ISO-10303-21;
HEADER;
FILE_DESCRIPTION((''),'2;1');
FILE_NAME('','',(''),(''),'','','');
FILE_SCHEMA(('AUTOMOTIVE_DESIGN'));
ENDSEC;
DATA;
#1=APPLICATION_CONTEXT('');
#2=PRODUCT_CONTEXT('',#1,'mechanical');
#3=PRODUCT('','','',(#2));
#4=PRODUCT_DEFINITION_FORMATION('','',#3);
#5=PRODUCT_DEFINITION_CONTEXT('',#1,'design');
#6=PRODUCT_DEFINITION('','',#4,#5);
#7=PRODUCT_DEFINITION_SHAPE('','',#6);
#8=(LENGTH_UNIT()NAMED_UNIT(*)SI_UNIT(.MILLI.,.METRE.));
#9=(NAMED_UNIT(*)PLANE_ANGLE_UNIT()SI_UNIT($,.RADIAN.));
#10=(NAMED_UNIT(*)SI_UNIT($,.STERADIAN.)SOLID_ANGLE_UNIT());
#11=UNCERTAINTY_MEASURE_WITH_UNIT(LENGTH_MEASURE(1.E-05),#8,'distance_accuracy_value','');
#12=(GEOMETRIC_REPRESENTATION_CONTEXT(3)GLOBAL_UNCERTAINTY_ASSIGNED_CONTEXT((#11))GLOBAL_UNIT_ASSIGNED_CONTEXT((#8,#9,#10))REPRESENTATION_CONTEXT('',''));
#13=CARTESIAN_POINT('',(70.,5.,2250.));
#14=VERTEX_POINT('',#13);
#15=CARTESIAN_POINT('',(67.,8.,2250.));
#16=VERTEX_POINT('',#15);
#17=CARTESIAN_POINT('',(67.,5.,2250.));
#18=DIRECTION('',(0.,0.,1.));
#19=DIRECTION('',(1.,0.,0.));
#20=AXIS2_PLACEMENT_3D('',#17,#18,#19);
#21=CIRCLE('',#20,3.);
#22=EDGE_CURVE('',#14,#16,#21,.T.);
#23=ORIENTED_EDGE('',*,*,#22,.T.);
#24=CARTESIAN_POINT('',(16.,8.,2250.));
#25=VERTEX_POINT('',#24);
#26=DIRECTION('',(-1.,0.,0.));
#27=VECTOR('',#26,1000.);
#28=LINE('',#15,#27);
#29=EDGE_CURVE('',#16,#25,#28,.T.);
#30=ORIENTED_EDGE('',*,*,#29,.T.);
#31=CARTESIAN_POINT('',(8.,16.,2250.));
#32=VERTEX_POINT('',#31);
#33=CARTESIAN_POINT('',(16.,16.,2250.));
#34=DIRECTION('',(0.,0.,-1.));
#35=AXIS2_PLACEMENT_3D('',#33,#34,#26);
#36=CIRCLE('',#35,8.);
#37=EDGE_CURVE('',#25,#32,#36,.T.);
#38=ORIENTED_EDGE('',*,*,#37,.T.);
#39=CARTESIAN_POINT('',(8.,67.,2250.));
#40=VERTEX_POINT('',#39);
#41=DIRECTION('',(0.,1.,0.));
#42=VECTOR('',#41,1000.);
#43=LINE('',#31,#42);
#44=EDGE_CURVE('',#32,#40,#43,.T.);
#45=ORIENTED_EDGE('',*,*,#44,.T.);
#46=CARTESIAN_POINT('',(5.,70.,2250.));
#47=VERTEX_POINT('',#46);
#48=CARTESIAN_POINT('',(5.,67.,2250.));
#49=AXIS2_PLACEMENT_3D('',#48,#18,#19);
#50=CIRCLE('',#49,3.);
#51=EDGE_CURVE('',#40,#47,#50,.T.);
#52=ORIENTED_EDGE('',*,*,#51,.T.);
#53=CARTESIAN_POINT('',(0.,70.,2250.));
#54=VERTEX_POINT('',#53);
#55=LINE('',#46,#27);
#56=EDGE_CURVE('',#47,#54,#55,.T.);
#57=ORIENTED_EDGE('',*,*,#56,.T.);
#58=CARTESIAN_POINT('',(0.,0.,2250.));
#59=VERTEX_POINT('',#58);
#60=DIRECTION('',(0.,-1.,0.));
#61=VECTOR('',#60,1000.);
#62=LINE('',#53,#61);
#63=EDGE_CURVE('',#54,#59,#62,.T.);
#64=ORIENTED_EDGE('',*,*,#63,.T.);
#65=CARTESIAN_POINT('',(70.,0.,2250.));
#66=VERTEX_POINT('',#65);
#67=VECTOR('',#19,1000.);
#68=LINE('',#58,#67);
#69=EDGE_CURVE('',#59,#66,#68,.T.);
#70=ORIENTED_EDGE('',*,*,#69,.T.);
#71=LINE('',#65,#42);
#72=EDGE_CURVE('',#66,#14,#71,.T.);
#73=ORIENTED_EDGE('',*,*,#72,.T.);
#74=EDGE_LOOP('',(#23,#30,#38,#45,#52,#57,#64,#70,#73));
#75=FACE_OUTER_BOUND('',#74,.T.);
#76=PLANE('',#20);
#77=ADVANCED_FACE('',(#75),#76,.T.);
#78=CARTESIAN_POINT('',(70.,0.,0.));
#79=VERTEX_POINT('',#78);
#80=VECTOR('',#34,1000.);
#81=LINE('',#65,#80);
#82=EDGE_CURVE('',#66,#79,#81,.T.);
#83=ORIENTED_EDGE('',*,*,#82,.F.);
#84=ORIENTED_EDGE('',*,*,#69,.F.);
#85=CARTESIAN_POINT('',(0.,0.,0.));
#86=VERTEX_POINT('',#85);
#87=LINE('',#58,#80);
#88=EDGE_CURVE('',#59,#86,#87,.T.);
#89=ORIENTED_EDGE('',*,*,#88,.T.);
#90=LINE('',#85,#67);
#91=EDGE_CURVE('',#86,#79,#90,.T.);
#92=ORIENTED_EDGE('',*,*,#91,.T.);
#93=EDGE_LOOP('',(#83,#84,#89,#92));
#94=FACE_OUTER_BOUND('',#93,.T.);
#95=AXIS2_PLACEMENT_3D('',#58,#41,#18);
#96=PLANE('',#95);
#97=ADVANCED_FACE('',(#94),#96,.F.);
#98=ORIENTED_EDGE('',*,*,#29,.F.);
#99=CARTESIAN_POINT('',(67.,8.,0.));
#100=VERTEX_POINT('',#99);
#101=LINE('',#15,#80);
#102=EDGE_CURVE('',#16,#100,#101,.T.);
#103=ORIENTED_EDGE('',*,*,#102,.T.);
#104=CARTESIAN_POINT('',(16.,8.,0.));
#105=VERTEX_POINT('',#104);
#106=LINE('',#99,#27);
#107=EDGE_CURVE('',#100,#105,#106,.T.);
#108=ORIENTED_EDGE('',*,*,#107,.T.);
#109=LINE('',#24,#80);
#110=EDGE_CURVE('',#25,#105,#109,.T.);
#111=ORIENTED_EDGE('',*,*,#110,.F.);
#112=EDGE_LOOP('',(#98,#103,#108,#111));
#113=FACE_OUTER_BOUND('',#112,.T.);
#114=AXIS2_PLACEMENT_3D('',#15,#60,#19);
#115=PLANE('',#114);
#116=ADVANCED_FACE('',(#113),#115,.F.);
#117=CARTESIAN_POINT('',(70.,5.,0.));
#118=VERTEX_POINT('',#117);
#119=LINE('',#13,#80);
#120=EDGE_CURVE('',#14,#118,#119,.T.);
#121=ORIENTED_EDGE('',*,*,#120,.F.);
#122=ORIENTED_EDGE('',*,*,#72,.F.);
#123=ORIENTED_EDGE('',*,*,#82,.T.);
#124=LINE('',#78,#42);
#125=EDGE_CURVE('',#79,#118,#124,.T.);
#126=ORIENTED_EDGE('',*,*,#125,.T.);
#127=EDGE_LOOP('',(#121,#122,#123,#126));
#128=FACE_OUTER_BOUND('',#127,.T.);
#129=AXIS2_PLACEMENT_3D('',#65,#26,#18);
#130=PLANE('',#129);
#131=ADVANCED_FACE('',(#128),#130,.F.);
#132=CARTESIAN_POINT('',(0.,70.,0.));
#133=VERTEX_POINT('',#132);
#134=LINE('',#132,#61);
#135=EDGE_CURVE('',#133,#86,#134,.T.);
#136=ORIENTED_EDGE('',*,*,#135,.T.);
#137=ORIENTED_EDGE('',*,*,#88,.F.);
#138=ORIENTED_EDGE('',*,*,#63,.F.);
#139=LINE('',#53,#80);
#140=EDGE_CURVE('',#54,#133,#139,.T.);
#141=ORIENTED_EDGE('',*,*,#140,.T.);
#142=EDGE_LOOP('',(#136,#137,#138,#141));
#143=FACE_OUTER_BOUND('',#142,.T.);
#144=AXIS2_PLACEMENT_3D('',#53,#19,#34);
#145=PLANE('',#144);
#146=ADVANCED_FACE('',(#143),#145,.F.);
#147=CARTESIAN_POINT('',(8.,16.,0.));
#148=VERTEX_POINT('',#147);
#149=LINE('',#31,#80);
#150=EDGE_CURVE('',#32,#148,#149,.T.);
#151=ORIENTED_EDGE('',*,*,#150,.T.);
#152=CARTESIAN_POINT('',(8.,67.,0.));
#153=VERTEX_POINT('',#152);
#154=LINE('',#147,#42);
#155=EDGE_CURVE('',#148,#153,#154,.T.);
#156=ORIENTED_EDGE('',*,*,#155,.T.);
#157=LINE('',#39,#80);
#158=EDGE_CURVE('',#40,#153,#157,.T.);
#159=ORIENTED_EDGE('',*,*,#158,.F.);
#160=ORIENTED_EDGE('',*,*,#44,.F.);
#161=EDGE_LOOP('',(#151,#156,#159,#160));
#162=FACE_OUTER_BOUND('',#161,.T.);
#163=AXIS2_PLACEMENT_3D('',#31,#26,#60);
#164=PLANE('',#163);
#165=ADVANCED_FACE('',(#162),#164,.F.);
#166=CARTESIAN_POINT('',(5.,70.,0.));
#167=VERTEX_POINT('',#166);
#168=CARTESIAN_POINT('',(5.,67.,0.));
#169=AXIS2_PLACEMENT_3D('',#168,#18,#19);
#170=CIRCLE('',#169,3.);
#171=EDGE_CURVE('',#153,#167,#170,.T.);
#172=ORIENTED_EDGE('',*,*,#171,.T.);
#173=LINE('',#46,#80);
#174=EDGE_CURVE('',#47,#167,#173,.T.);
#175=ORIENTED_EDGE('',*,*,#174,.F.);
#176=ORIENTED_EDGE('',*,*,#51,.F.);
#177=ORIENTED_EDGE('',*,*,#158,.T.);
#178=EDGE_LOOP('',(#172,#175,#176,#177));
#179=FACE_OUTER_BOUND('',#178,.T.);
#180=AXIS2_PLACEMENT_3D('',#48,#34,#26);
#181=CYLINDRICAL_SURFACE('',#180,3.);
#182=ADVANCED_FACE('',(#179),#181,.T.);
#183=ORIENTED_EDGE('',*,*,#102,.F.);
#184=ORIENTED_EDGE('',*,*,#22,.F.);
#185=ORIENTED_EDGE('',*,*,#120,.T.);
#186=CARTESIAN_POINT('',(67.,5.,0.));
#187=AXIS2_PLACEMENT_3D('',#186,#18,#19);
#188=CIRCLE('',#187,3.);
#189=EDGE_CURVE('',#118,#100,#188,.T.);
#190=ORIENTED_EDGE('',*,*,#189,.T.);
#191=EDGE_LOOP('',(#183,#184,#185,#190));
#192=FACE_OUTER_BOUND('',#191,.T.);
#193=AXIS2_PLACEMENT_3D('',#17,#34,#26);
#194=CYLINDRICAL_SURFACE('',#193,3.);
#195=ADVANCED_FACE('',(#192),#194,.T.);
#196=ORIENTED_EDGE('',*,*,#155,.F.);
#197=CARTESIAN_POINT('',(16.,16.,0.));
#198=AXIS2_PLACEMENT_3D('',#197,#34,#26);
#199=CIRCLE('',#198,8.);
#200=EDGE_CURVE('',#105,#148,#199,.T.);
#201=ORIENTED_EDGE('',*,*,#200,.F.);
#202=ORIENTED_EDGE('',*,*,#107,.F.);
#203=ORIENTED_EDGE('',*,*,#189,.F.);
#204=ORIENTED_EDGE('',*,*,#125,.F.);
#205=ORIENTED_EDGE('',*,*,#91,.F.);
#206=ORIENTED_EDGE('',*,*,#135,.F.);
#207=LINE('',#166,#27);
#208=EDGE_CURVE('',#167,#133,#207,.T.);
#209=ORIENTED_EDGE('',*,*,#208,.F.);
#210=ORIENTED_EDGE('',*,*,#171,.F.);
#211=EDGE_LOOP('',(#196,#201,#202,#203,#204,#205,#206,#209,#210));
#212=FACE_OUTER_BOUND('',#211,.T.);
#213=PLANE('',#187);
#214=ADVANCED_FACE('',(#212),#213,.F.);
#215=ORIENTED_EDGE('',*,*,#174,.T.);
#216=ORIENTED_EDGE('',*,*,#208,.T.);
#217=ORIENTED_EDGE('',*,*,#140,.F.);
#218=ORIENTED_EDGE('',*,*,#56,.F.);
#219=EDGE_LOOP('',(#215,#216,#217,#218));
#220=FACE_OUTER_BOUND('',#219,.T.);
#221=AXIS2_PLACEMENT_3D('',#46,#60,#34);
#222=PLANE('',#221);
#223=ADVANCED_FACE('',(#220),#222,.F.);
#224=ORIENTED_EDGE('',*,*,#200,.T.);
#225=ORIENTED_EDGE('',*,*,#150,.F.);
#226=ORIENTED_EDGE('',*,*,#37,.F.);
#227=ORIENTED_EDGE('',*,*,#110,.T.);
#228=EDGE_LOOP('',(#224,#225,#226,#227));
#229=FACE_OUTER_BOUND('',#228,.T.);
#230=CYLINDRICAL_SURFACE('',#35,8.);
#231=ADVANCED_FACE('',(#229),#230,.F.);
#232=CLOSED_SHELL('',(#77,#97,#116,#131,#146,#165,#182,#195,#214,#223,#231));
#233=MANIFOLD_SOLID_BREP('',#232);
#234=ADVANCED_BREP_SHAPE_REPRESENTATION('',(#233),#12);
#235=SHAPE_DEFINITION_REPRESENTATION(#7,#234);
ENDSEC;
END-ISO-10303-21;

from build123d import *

# Parameters (mm, degrees)
BOSS_EXTRUDE1_DEPTH = 2250


with BuildPart() as part:
    # Sketch1 → Boss-Extrude1 (new body)
    with BuildSketch(Plane.XY):
        with BuildLine():
            Line((0, 70), (0, 0))
            Line((0, 0), (70, 0))
            Line((70, 0), (70, 5))
            ThreePointArc((70, 5), (69.121320344, 7.121320344), (67, 8))
            Line((67, 8), (16, 8))
            ThreePointArc((16, 8), (10.343145751, 10.343145751), (8, 16))
            Line((8, 16), (8, 67))
            ThreePointArc((8, 67), (7.121320344, 69.121320344), (5, 70))
            Line((5, 70), (0, 70))
        make_face()
    extrude(amount=BOSS_EXTRUDE1_DEPTH)


solid = part.part
